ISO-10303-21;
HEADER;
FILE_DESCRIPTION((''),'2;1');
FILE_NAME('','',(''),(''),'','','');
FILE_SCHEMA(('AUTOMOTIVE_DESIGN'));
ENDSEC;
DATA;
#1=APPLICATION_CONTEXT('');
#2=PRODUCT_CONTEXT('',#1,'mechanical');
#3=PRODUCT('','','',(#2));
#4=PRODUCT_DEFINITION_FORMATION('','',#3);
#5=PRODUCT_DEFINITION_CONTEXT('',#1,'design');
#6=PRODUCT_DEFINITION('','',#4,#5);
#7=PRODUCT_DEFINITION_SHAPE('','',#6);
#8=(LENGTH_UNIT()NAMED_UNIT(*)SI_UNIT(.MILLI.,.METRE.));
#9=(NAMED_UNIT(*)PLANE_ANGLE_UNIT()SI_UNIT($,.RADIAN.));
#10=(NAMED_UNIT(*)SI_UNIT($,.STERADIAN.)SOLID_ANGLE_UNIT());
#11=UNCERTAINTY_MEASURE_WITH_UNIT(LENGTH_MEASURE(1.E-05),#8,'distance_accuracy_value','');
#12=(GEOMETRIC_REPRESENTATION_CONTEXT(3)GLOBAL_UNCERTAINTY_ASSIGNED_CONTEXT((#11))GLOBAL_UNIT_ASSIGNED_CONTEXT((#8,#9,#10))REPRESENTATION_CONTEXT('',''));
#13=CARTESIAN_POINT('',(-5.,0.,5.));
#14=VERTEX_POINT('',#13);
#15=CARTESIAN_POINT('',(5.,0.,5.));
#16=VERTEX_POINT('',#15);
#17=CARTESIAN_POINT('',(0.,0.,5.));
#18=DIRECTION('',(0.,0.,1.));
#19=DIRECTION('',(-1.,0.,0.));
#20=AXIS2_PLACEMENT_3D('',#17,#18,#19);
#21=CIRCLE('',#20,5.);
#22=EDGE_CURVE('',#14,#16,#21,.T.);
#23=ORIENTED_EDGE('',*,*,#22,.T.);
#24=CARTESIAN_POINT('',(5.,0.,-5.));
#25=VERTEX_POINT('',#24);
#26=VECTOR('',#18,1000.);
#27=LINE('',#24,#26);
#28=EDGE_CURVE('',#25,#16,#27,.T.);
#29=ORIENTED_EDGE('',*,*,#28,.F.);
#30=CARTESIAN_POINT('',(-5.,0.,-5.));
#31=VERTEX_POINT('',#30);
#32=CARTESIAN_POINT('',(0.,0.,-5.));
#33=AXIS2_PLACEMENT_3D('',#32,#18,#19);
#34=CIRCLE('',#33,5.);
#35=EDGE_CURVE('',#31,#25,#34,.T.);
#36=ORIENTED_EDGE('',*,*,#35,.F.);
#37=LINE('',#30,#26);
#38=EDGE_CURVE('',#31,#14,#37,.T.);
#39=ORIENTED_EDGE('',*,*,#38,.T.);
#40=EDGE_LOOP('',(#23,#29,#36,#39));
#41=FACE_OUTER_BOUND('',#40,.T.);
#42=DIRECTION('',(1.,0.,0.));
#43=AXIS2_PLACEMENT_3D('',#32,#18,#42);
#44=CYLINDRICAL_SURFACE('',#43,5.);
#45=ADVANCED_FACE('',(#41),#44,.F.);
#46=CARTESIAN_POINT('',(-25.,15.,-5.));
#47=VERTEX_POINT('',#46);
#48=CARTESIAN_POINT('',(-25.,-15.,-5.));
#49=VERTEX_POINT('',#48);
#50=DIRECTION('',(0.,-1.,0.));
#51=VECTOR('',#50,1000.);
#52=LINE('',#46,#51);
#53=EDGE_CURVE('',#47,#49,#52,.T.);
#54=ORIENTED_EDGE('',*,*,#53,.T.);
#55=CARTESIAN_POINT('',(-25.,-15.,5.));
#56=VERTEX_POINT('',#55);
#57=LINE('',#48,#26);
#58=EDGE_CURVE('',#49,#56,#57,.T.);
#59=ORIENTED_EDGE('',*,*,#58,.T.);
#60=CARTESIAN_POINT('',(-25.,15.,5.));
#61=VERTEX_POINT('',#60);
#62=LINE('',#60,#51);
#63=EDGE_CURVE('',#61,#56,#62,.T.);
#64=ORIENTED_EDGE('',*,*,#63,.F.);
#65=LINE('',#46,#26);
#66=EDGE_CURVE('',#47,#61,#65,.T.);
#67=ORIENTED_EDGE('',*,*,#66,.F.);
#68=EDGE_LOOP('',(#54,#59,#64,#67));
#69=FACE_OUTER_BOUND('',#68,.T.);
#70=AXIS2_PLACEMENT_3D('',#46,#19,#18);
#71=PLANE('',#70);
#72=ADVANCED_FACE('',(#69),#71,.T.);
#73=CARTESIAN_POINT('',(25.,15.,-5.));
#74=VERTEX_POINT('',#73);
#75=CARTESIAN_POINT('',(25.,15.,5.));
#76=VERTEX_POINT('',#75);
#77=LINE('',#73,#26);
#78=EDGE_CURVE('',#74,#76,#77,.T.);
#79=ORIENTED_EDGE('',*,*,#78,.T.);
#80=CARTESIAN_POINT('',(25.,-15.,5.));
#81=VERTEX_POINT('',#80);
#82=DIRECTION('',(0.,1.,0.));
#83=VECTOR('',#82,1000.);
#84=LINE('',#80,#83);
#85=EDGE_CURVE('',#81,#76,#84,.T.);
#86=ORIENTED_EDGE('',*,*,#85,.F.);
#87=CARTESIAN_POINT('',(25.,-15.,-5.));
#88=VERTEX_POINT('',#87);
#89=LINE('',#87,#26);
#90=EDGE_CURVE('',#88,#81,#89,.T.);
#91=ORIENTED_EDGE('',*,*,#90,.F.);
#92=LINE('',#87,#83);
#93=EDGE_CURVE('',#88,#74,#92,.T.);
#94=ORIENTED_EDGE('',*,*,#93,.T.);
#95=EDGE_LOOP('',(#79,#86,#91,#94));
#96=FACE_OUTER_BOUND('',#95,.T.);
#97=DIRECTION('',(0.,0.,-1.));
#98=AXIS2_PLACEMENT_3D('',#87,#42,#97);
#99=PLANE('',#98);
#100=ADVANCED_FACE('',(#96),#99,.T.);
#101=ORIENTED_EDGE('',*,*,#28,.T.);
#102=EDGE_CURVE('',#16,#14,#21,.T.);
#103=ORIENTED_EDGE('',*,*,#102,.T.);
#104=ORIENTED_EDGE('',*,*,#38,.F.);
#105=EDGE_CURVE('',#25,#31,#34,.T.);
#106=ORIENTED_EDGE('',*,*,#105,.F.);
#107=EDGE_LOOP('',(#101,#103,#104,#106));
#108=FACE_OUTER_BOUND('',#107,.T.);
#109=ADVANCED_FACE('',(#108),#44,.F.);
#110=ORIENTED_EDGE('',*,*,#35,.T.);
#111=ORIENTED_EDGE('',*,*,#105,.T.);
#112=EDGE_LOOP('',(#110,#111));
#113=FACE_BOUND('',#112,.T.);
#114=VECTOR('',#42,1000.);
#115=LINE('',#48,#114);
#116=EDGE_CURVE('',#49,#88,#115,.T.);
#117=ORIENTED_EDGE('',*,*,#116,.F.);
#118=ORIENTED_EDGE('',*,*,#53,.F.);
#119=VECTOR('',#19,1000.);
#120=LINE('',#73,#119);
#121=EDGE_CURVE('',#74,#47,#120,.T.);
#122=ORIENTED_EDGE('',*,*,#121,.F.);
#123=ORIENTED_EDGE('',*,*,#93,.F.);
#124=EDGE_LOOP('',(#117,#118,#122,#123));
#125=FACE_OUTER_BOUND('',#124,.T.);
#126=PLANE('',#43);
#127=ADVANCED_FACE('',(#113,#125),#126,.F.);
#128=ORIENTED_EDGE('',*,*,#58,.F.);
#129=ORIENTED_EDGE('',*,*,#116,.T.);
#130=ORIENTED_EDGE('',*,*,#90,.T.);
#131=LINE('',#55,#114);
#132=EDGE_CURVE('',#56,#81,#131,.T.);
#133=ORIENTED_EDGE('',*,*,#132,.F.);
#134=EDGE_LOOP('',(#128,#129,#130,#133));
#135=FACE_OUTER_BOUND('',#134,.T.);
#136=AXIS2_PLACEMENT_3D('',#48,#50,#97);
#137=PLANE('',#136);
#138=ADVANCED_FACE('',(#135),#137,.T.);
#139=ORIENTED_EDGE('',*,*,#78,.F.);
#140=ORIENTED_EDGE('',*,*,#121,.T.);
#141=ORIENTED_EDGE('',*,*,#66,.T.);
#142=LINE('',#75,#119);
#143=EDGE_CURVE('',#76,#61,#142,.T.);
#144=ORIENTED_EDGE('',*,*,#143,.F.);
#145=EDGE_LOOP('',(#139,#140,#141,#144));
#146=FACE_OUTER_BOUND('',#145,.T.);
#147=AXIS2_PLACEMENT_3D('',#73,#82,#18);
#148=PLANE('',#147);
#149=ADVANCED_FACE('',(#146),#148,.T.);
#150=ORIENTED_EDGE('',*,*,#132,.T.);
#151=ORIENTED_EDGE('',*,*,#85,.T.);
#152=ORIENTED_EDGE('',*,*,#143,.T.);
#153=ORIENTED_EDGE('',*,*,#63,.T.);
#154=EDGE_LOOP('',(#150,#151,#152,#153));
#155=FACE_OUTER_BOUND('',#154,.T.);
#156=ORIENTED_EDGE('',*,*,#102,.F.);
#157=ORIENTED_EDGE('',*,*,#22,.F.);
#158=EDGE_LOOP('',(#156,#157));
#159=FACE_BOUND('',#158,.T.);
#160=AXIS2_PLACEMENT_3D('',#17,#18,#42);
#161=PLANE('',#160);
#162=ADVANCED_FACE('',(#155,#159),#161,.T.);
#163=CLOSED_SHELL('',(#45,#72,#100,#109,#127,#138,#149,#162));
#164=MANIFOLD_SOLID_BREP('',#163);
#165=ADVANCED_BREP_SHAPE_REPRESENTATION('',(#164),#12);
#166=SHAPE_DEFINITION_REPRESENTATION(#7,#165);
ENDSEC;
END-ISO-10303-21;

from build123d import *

# Parameters (mm, degrees)
SKETCH1_W           = 50
SKETCH1_H           = 30
SKETCH1_R           = 5
BOSS_EXTRUDE1_DEPTH = 10


with BuildPart() as part:
    # Sketch1 → Boss-Extrude1 (new body)
    with BuildSketch(Plane.XY.offset(5)):
        Rectangle(SKETCH1_W, SKETCH1_H)
        with Locations(Location((0, 0, 0), (0, 0, 180))):
            Circle(SKETCH1_R, mode=Mode.SUBTRACT)
    extrude(amount=-BOSS_EXTRUDE1_DEPTH)


solid = part.part
